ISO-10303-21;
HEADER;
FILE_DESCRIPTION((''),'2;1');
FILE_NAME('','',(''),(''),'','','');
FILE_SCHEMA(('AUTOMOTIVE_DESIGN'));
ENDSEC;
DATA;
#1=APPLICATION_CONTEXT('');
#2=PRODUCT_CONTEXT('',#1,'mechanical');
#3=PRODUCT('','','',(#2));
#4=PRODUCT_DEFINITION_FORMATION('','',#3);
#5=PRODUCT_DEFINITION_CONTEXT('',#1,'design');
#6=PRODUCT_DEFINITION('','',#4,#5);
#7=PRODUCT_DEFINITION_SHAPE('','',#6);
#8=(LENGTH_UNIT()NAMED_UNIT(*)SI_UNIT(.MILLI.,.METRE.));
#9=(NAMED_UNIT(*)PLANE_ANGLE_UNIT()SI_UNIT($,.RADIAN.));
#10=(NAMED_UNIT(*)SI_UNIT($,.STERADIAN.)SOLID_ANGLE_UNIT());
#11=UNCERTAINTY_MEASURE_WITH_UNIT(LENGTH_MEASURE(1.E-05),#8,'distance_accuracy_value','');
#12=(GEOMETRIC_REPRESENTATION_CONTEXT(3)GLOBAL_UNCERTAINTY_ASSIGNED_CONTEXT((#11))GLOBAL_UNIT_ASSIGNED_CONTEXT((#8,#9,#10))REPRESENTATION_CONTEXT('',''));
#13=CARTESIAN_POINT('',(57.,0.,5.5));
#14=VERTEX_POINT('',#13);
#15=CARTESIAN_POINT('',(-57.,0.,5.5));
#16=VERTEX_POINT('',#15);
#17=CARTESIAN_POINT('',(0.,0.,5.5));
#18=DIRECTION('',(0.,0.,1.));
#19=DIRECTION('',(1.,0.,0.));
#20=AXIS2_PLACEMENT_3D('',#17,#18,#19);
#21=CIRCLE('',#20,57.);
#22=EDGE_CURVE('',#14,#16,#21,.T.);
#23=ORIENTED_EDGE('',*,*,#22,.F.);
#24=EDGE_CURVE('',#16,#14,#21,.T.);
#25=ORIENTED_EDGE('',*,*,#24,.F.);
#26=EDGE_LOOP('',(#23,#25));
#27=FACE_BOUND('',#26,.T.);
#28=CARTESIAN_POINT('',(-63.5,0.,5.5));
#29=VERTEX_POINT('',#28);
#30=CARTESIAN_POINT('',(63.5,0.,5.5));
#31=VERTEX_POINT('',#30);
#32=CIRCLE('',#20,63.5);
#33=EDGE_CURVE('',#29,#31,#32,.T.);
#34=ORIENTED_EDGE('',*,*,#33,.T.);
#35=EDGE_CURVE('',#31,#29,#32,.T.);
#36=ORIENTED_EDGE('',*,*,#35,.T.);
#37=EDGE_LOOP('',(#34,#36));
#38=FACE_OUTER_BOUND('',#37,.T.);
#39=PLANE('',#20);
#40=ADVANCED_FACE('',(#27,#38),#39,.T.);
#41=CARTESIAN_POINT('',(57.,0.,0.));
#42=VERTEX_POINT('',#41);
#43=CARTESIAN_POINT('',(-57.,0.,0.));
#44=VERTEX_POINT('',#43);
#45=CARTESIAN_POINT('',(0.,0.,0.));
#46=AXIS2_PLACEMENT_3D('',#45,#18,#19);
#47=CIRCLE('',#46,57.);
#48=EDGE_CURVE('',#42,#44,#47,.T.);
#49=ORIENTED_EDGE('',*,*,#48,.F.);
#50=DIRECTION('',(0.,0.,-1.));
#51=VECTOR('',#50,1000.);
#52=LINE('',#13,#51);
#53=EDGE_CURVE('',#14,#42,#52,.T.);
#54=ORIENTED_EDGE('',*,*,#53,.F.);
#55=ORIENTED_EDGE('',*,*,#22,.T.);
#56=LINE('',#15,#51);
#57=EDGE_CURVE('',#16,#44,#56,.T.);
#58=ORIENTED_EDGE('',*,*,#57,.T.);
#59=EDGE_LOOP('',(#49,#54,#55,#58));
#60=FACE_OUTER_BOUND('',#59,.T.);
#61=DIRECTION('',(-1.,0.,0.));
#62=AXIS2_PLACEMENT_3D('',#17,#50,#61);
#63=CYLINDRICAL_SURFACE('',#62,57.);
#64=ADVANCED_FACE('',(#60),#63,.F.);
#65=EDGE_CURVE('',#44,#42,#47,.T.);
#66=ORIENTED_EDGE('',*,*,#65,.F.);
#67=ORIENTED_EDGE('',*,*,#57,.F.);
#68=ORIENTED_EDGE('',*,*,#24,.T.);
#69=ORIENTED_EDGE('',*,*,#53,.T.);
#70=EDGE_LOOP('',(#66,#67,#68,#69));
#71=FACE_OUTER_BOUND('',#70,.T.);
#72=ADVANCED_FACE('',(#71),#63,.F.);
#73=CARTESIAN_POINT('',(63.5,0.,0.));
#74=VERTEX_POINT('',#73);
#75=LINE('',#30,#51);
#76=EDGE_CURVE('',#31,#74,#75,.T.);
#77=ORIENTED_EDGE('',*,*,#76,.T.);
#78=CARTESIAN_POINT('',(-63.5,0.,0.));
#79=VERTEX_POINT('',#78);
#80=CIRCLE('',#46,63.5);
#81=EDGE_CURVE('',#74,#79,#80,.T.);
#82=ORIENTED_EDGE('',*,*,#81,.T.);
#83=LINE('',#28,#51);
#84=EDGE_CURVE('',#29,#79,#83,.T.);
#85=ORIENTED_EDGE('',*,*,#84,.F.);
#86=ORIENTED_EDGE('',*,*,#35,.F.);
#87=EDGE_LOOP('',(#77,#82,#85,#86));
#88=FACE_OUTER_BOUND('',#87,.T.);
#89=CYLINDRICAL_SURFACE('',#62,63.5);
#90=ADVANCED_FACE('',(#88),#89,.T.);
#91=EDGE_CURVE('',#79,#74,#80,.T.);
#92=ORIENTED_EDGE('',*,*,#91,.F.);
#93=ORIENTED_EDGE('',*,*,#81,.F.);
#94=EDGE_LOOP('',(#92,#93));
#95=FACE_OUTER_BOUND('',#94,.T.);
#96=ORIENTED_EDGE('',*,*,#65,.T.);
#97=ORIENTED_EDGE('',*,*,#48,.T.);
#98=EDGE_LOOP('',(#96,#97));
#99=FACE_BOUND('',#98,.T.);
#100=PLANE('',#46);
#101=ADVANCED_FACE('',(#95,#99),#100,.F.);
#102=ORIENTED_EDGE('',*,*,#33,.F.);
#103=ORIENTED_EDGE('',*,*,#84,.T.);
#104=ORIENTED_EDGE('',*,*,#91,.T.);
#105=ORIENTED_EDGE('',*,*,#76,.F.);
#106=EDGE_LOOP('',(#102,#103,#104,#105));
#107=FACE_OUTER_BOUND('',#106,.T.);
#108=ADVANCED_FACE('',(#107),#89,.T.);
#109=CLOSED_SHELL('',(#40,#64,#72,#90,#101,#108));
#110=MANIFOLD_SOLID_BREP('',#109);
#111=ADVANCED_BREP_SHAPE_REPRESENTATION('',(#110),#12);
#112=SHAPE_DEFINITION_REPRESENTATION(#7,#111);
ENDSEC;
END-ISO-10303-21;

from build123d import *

# Parameters (mm, degrees)
SKETCH1_R           = 63.5
SKETCH1_R_2         = 57
BOSS_EXTRUDE1_DEPTH = 5.5


with BuildPart() as part:
    # Sketch1 → Boss-Extrude1 (new body)
    with BuildSketch(Plane.XY):
        Circle(SKETCH1_R)
        Circle(SKETCH1_R_2, mode=Mode.SUBTRACT)
    extrude(amount=BOSS_EXTRUDE1_DEPTH)


solid = part.part
